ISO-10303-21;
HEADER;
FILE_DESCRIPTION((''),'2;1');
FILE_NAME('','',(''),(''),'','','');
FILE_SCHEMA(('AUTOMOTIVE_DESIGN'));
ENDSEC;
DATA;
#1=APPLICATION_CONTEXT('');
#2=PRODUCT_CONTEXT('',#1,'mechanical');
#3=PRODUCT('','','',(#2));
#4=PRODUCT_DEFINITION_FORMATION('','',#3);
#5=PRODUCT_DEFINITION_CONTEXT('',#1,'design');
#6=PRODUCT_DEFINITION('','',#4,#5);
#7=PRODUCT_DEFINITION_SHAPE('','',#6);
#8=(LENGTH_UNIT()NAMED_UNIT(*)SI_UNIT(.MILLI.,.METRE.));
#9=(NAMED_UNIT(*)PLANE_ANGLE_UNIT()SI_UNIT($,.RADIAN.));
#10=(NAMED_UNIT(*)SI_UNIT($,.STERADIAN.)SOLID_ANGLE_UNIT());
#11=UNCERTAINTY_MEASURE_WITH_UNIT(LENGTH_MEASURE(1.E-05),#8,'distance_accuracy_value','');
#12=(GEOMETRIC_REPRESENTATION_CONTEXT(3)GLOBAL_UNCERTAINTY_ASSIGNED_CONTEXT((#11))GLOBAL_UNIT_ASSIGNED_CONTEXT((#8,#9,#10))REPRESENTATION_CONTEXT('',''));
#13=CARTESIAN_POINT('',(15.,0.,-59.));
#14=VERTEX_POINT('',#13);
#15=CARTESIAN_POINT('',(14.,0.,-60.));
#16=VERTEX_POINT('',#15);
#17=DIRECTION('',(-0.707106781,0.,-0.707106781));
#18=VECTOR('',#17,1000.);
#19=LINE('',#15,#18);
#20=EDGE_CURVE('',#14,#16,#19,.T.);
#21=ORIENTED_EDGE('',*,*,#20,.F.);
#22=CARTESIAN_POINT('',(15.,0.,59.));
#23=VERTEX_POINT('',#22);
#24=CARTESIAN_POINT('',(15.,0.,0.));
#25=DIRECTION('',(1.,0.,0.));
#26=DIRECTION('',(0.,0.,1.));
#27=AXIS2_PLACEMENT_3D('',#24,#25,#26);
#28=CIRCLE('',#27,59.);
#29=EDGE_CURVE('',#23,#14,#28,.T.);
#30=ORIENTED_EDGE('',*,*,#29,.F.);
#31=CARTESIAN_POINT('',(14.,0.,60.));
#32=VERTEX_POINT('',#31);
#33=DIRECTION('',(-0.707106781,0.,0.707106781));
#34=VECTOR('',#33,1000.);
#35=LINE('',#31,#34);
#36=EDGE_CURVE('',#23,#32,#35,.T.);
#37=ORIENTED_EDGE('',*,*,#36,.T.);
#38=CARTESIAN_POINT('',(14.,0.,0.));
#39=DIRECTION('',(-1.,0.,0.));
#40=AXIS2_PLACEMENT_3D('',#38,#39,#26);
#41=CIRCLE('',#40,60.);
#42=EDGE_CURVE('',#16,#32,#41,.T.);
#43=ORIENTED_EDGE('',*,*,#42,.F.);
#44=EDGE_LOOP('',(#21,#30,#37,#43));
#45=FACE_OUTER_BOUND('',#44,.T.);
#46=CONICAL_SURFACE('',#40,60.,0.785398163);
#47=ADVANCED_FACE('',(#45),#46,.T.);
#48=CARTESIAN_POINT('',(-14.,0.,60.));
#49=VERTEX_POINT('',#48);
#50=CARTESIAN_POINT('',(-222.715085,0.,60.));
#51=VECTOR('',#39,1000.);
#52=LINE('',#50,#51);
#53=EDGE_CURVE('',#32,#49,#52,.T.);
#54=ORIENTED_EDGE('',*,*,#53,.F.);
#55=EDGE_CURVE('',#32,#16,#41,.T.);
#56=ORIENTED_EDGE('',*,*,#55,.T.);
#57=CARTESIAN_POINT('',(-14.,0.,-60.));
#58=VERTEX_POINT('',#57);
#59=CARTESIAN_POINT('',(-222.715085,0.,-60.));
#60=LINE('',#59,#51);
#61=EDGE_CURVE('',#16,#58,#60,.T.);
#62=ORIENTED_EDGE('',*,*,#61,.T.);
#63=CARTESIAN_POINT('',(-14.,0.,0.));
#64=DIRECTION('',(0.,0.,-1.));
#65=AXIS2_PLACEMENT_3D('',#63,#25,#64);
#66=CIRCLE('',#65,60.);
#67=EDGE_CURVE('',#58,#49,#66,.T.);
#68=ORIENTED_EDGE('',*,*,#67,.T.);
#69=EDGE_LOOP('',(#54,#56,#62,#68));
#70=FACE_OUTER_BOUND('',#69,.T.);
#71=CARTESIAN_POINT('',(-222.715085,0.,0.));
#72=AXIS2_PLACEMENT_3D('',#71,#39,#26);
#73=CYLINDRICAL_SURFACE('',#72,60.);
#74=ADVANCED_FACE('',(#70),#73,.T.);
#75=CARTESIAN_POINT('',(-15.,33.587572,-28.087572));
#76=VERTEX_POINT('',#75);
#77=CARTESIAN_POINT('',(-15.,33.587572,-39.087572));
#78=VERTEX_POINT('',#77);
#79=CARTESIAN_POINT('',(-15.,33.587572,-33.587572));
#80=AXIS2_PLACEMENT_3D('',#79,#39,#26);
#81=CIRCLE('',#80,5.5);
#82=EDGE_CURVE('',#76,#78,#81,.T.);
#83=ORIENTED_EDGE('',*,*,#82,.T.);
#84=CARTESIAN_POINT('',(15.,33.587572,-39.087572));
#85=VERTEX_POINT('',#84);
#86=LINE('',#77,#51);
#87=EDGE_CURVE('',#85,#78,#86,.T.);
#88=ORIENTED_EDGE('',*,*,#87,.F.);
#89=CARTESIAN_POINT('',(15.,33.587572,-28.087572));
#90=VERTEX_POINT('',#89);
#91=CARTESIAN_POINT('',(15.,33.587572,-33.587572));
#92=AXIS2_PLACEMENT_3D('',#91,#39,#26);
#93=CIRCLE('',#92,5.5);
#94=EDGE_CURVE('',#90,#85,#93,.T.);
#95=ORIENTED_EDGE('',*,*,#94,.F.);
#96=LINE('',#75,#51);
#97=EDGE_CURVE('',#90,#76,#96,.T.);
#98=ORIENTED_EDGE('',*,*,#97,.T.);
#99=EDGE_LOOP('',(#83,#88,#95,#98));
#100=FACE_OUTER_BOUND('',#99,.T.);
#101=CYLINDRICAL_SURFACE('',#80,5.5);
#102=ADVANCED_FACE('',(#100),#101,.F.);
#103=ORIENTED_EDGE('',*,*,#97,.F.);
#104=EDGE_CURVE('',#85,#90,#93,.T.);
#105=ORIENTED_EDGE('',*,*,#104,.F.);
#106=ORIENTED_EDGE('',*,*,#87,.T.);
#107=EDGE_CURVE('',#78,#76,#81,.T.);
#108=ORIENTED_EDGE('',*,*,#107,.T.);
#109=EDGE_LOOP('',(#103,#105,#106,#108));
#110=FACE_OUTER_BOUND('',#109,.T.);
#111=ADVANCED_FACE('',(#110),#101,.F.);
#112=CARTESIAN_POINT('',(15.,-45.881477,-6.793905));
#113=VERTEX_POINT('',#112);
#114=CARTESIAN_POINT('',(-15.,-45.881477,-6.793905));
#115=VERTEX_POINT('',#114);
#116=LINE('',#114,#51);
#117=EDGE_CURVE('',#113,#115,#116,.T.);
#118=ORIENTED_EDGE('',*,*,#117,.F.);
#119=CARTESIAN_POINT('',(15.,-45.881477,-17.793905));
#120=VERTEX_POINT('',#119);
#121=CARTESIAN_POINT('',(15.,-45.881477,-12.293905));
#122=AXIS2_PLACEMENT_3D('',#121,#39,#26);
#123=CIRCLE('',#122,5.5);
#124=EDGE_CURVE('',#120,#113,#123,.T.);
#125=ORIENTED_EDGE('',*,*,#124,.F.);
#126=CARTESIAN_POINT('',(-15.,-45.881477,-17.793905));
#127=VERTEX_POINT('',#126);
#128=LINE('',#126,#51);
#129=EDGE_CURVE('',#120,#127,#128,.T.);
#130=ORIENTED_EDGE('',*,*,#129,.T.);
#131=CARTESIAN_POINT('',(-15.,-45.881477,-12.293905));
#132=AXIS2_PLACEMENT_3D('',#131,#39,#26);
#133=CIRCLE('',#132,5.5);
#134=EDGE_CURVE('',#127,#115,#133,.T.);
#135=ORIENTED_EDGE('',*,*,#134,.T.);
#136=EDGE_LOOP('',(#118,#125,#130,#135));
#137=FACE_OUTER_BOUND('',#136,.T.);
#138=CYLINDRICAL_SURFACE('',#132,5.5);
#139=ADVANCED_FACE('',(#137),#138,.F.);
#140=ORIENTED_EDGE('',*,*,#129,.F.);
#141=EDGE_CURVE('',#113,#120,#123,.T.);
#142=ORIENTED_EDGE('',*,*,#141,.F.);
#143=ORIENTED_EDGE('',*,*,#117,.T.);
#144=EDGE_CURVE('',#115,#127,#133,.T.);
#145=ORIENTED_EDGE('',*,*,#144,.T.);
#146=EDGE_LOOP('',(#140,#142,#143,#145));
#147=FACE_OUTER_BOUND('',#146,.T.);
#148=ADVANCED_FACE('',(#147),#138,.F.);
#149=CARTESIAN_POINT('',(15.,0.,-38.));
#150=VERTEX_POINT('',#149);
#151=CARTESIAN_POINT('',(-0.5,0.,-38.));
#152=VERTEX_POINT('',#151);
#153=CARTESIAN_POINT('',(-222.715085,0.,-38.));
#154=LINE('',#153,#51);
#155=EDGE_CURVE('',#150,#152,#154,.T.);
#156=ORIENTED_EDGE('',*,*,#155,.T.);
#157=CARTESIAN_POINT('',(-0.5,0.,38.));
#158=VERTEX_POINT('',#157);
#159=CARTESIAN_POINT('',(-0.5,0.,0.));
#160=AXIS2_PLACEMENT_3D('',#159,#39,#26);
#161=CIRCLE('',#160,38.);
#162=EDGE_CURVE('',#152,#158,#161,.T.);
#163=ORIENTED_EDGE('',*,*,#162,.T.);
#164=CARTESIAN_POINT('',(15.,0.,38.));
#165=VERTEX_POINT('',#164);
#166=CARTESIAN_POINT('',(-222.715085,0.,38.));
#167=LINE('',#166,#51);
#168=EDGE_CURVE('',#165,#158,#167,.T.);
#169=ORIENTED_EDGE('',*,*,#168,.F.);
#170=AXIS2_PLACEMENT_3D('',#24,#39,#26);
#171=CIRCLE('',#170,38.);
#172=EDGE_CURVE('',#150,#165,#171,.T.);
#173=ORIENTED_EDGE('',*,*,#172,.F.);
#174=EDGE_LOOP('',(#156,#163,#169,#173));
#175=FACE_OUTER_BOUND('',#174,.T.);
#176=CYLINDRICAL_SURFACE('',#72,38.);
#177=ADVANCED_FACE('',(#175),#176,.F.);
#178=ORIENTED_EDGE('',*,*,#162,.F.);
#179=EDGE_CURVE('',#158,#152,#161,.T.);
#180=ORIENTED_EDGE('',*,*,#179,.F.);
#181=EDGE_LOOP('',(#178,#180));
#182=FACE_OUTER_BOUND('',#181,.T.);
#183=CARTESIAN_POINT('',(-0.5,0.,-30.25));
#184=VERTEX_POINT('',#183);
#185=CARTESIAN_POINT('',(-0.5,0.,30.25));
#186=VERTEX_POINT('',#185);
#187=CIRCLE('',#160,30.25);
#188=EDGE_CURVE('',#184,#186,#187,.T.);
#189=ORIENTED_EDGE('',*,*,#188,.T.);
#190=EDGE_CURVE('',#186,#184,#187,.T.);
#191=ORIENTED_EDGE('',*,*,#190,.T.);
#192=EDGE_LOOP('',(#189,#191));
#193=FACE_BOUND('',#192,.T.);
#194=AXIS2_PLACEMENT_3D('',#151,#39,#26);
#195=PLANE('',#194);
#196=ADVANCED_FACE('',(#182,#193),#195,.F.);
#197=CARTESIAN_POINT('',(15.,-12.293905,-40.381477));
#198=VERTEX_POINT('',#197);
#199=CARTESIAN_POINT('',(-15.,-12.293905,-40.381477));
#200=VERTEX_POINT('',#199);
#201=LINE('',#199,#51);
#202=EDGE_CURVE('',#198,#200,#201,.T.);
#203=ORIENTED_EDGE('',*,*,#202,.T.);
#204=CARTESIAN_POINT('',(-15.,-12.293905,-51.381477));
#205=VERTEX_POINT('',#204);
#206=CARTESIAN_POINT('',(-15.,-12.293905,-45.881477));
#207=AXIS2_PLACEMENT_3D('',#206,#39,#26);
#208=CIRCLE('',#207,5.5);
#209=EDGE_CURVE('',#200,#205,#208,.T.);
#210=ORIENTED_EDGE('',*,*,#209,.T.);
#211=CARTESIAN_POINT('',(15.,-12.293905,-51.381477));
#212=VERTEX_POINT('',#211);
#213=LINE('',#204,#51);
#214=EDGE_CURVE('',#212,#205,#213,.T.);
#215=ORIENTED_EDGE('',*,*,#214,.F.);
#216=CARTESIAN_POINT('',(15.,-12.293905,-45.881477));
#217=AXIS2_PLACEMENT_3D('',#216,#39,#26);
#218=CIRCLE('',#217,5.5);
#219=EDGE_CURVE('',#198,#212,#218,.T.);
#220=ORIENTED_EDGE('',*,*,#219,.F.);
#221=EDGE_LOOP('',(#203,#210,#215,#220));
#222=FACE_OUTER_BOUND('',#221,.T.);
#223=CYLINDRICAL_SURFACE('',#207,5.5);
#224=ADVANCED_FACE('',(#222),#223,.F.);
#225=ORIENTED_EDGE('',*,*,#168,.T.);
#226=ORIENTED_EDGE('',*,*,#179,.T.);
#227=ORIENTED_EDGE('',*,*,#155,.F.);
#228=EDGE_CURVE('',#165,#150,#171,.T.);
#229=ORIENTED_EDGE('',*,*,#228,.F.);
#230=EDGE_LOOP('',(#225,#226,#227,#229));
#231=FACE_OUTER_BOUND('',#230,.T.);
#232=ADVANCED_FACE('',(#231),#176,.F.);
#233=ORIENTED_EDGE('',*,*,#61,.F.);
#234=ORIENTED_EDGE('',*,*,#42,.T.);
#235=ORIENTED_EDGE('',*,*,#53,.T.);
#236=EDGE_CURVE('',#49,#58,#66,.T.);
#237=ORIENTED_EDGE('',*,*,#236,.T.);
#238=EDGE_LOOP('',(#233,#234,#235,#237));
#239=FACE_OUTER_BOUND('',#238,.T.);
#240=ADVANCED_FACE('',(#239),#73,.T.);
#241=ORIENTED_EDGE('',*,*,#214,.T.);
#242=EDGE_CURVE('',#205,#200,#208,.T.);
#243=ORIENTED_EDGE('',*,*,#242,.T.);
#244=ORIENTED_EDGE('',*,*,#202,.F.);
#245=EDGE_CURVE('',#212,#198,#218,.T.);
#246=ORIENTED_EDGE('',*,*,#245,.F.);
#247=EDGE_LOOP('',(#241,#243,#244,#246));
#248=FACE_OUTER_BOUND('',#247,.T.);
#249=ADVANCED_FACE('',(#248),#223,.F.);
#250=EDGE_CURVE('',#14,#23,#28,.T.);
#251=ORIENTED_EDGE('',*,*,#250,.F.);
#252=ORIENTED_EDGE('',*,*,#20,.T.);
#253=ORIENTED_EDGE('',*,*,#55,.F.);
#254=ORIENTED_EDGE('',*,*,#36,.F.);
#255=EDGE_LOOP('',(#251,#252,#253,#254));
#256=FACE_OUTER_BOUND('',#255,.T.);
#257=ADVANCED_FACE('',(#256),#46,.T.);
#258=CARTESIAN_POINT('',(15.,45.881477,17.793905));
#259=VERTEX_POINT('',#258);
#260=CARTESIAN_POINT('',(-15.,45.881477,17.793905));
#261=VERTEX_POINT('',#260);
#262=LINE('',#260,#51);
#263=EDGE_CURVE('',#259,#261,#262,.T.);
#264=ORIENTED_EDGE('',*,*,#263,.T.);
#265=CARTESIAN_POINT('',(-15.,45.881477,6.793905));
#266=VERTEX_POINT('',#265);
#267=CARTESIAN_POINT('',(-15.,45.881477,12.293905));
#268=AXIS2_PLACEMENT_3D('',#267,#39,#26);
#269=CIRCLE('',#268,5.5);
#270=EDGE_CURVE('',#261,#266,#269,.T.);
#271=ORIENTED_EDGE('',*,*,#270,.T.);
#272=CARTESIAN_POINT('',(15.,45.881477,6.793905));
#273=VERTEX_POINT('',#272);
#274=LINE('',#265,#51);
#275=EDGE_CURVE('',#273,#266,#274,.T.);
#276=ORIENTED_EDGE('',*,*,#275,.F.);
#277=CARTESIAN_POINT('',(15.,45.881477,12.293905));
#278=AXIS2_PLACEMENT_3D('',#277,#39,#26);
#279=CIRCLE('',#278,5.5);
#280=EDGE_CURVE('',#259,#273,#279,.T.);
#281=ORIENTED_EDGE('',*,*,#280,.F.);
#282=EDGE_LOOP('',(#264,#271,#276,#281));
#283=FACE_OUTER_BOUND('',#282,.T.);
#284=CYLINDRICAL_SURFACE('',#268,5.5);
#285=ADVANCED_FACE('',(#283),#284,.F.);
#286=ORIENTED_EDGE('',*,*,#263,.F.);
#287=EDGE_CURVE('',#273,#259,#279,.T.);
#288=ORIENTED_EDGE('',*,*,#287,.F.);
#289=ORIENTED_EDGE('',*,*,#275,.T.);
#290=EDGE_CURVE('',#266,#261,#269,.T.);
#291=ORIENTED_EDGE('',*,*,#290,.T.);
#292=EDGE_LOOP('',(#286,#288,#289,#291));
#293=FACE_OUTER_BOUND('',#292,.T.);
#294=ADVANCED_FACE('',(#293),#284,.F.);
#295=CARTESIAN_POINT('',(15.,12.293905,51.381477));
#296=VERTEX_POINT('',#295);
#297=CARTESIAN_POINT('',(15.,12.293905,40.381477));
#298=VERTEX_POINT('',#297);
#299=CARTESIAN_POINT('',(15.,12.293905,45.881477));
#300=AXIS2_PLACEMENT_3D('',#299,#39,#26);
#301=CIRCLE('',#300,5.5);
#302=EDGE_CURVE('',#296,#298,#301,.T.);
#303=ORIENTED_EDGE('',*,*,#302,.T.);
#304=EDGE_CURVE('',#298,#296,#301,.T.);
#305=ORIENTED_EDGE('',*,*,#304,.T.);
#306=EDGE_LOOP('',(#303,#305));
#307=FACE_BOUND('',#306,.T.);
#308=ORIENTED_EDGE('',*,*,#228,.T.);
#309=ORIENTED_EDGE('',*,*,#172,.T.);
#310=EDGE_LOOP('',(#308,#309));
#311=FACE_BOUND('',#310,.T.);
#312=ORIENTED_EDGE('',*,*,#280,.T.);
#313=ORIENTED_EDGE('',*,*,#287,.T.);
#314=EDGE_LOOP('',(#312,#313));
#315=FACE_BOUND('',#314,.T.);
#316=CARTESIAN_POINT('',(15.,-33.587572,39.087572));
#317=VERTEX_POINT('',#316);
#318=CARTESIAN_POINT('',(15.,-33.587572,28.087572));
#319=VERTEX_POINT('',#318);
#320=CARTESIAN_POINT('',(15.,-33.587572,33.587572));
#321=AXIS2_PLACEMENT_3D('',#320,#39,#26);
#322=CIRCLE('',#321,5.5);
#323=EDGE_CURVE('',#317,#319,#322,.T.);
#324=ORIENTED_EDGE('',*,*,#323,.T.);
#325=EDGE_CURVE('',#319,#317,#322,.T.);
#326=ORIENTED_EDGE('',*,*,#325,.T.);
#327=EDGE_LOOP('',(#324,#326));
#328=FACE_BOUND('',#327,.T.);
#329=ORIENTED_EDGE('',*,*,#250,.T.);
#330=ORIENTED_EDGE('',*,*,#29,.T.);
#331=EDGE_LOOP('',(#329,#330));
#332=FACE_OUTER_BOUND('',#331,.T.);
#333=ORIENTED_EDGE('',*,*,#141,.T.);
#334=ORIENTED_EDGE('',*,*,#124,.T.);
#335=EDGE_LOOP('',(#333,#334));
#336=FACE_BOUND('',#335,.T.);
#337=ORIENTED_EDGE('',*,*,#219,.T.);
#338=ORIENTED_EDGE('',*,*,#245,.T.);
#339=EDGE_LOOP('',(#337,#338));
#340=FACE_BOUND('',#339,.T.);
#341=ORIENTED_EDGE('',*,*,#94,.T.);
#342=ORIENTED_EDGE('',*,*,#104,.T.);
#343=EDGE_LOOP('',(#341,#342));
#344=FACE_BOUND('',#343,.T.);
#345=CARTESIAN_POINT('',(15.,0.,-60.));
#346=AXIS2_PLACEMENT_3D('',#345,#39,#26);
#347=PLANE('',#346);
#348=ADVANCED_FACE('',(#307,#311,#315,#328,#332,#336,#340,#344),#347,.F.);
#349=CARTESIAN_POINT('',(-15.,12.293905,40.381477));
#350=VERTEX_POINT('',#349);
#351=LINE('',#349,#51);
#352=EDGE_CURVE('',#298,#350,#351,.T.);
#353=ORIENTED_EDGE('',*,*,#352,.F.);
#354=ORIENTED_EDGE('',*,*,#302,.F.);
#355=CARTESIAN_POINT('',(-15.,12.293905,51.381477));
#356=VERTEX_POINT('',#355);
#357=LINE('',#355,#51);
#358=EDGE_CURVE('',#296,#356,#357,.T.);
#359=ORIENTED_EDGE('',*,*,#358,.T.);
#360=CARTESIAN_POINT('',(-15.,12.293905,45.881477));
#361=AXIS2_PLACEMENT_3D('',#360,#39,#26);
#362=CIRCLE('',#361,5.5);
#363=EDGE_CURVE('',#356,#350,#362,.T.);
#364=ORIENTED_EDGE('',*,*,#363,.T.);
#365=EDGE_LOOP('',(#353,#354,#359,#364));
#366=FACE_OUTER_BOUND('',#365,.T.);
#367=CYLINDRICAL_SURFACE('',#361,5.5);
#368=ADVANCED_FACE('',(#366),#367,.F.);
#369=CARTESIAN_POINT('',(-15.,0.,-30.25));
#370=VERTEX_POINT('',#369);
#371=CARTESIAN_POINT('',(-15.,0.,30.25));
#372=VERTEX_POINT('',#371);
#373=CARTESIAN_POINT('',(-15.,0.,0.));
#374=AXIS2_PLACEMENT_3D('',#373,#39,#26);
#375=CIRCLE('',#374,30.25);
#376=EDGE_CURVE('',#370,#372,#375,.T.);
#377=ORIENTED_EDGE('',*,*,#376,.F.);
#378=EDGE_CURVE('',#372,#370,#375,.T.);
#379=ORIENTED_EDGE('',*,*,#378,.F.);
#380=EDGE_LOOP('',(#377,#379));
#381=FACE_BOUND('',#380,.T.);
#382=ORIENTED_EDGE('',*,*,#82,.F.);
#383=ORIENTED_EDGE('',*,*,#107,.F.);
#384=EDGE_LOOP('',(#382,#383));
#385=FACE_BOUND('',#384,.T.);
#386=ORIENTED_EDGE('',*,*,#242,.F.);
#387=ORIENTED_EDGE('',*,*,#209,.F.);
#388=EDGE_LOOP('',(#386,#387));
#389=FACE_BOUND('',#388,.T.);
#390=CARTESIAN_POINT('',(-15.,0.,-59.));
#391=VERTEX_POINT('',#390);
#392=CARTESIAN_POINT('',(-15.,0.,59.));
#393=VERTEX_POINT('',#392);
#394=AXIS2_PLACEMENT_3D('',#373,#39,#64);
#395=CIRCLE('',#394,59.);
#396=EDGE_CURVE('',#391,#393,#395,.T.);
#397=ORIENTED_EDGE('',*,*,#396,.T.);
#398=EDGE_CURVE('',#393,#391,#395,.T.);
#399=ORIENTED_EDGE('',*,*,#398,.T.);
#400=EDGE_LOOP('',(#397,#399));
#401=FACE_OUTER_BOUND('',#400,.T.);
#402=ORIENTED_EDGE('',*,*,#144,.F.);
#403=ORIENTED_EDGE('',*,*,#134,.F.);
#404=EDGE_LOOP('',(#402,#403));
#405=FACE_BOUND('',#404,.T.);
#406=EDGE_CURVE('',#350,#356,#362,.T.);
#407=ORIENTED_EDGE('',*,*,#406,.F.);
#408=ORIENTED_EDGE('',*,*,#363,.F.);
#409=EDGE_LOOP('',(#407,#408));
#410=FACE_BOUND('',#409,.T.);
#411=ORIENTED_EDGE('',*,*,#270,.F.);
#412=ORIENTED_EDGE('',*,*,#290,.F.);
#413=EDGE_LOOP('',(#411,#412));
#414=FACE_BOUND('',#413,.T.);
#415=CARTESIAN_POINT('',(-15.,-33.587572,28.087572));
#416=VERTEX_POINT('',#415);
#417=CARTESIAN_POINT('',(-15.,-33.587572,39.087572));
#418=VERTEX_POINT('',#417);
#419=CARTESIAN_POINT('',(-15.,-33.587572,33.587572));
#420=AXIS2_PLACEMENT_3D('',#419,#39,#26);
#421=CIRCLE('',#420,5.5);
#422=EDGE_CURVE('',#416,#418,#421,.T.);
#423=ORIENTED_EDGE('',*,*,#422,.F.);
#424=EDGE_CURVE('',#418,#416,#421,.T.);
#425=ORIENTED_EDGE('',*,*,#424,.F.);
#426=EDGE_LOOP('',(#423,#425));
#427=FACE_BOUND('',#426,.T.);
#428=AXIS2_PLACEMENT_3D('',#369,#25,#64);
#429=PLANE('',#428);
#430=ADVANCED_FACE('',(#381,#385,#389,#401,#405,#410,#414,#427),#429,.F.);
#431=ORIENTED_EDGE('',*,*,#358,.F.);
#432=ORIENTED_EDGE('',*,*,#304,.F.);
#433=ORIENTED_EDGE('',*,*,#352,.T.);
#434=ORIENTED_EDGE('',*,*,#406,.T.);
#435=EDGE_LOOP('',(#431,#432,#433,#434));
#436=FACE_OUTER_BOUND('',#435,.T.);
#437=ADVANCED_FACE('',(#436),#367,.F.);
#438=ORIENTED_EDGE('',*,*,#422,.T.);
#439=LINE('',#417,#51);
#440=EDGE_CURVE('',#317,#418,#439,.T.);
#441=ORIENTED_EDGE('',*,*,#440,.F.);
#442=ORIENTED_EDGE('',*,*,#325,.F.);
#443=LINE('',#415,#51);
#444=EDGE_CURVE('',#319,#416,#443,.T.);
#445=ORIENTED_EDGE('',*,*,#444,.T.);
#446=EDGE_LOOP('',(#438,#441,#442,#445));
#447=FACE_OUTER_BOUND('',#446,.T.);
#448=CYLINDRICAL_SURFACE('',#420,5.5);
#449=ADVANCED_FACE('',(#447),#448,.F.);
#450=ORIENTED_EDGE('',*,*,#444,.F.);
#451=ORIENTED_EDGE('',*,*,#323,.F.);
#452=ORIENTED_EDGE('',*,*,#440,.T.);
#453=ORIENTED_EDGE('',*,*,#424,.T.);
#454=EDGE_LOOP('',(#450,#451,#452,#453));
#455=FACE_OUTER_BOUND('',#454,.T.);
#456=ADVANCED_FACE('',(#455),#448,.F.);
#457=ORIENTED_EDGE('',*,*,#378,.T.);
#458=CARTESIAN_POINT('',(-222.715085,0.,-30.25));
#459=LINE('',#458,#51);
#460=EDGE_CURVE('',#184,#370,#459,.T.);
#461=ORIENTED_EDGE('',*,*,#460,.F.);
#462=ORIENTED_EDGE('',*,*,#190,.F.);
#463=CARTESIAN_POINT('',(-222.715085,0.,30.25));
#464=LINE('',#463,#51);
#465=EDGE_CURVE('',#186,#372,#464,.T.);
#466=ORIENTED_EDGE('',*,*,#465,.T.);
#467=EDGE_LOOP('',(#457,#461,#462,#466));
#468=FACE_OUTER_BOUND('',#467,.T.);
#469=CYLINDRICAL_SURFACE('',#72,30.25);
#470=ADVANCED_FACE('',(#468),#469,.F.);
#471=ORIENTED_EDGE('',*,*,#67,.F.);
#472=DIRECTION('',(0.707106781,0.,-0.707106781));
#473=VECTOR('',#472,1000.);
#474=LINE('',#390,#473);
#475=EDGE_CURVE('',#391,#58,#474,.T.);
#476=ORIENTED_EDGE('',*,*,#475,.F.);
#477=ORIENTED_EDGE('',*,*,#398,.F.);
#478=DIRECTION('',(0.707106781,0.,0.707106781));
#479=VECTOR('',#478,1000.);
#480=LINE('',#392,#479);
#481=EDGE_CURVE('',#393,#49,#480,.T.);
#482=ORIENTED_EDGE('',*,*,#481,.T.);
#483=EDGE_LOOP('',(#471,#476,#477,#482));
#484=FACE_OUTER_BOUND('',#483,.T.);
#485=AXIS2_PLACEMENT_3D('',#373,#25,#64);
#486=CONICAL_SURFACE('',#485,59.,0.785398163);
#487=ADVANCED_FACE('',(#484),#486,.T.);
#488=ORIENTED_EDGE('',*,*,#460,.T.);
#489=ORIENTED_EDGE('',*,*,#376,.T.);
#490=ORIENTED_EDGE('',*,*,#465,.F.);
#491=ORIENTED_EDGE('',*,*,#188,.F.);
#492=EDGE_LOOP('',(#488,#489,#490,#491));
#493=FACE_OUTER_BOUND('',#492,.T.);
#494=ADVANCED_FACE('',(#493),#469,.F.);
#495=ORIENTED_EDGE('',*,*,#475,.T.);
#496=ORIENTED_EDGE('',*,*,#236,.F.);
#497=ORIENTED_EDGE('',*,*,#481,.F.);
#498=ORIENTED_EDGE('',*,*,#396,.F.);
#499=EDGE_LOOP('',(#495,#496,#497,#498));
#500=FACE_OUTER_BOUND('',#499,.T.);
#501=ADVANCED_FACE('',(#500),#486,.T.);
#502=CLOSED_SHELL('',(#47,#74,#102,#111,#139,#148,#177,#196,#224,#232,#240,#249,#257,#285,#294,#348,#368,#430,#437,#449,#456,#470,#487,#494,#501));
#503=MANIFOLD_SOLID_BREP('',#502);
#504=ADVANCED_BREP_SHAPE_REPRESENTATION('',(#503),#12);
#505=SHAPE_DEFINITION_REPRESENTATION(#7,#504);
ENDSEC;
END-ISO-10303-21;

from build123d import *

# Parameters (mm, degrees)
CHAMFER_1_SIZE           = 1
HOLE_WIZARD_M10_1_D      = 11
PATTERN_CIRCULAR_1_COUNT = 6


with BuildPart() as part:
    # 草图1 → 旋转1 (revolve)
    with BuildSketch(Plane(origin=(0, 0, 0), x_dir=(1, 0, 0), z_dir=(0, 1, 0)), mode=Mode.PRIVATE) as revolve_1_sk:
        Polygon((-15, 60), (15, 60), (15, 38), (-0.5, 38), (-0.5, 30.25), (-15, 30.25), align=None)
    revolve(revolve_1_sk.sketch.rotate(Axis((-222.715084562, 0, 0), (1, 0, 0)), 180), axis=Axis((-222.715084562, 0, 0), (1, 0, 0)))

    # 倒角1
    chamfer_1_edges = [part.edges().sort_by_distance(p)[0] for p in [
        (15, 0, -60),
        (-15, 0, -60),
    ]]
    chamfer(chamfer_1_edges, length=CHAMFER_1_SIZE)

    # M10 间隙孔1 (through all)
    with Locations(Plane.ZY.offset(15)):
        with Locations((33.587572106, -33.587572106)):
            hole_wizard_m10_1 = Hole(HOLE_WIZARD_M10_1_D / 2)

    # 阵列(圆周)1: M10 间隙孔1 ×6 about axis
    pattern_circular_1_axis = Axis((0, 0, 0), (1, 0, 0))
    for i in range(1, PATTERN_CIRCULAR_1_COUNT):
        add(hole_wizard_m10_1.rotate(pattern_circular_1_axis, i * 360 / PATTERN_CIRCULAR_1_COUNT), mode=Mode.SUBTRACT)


solid = part.part
